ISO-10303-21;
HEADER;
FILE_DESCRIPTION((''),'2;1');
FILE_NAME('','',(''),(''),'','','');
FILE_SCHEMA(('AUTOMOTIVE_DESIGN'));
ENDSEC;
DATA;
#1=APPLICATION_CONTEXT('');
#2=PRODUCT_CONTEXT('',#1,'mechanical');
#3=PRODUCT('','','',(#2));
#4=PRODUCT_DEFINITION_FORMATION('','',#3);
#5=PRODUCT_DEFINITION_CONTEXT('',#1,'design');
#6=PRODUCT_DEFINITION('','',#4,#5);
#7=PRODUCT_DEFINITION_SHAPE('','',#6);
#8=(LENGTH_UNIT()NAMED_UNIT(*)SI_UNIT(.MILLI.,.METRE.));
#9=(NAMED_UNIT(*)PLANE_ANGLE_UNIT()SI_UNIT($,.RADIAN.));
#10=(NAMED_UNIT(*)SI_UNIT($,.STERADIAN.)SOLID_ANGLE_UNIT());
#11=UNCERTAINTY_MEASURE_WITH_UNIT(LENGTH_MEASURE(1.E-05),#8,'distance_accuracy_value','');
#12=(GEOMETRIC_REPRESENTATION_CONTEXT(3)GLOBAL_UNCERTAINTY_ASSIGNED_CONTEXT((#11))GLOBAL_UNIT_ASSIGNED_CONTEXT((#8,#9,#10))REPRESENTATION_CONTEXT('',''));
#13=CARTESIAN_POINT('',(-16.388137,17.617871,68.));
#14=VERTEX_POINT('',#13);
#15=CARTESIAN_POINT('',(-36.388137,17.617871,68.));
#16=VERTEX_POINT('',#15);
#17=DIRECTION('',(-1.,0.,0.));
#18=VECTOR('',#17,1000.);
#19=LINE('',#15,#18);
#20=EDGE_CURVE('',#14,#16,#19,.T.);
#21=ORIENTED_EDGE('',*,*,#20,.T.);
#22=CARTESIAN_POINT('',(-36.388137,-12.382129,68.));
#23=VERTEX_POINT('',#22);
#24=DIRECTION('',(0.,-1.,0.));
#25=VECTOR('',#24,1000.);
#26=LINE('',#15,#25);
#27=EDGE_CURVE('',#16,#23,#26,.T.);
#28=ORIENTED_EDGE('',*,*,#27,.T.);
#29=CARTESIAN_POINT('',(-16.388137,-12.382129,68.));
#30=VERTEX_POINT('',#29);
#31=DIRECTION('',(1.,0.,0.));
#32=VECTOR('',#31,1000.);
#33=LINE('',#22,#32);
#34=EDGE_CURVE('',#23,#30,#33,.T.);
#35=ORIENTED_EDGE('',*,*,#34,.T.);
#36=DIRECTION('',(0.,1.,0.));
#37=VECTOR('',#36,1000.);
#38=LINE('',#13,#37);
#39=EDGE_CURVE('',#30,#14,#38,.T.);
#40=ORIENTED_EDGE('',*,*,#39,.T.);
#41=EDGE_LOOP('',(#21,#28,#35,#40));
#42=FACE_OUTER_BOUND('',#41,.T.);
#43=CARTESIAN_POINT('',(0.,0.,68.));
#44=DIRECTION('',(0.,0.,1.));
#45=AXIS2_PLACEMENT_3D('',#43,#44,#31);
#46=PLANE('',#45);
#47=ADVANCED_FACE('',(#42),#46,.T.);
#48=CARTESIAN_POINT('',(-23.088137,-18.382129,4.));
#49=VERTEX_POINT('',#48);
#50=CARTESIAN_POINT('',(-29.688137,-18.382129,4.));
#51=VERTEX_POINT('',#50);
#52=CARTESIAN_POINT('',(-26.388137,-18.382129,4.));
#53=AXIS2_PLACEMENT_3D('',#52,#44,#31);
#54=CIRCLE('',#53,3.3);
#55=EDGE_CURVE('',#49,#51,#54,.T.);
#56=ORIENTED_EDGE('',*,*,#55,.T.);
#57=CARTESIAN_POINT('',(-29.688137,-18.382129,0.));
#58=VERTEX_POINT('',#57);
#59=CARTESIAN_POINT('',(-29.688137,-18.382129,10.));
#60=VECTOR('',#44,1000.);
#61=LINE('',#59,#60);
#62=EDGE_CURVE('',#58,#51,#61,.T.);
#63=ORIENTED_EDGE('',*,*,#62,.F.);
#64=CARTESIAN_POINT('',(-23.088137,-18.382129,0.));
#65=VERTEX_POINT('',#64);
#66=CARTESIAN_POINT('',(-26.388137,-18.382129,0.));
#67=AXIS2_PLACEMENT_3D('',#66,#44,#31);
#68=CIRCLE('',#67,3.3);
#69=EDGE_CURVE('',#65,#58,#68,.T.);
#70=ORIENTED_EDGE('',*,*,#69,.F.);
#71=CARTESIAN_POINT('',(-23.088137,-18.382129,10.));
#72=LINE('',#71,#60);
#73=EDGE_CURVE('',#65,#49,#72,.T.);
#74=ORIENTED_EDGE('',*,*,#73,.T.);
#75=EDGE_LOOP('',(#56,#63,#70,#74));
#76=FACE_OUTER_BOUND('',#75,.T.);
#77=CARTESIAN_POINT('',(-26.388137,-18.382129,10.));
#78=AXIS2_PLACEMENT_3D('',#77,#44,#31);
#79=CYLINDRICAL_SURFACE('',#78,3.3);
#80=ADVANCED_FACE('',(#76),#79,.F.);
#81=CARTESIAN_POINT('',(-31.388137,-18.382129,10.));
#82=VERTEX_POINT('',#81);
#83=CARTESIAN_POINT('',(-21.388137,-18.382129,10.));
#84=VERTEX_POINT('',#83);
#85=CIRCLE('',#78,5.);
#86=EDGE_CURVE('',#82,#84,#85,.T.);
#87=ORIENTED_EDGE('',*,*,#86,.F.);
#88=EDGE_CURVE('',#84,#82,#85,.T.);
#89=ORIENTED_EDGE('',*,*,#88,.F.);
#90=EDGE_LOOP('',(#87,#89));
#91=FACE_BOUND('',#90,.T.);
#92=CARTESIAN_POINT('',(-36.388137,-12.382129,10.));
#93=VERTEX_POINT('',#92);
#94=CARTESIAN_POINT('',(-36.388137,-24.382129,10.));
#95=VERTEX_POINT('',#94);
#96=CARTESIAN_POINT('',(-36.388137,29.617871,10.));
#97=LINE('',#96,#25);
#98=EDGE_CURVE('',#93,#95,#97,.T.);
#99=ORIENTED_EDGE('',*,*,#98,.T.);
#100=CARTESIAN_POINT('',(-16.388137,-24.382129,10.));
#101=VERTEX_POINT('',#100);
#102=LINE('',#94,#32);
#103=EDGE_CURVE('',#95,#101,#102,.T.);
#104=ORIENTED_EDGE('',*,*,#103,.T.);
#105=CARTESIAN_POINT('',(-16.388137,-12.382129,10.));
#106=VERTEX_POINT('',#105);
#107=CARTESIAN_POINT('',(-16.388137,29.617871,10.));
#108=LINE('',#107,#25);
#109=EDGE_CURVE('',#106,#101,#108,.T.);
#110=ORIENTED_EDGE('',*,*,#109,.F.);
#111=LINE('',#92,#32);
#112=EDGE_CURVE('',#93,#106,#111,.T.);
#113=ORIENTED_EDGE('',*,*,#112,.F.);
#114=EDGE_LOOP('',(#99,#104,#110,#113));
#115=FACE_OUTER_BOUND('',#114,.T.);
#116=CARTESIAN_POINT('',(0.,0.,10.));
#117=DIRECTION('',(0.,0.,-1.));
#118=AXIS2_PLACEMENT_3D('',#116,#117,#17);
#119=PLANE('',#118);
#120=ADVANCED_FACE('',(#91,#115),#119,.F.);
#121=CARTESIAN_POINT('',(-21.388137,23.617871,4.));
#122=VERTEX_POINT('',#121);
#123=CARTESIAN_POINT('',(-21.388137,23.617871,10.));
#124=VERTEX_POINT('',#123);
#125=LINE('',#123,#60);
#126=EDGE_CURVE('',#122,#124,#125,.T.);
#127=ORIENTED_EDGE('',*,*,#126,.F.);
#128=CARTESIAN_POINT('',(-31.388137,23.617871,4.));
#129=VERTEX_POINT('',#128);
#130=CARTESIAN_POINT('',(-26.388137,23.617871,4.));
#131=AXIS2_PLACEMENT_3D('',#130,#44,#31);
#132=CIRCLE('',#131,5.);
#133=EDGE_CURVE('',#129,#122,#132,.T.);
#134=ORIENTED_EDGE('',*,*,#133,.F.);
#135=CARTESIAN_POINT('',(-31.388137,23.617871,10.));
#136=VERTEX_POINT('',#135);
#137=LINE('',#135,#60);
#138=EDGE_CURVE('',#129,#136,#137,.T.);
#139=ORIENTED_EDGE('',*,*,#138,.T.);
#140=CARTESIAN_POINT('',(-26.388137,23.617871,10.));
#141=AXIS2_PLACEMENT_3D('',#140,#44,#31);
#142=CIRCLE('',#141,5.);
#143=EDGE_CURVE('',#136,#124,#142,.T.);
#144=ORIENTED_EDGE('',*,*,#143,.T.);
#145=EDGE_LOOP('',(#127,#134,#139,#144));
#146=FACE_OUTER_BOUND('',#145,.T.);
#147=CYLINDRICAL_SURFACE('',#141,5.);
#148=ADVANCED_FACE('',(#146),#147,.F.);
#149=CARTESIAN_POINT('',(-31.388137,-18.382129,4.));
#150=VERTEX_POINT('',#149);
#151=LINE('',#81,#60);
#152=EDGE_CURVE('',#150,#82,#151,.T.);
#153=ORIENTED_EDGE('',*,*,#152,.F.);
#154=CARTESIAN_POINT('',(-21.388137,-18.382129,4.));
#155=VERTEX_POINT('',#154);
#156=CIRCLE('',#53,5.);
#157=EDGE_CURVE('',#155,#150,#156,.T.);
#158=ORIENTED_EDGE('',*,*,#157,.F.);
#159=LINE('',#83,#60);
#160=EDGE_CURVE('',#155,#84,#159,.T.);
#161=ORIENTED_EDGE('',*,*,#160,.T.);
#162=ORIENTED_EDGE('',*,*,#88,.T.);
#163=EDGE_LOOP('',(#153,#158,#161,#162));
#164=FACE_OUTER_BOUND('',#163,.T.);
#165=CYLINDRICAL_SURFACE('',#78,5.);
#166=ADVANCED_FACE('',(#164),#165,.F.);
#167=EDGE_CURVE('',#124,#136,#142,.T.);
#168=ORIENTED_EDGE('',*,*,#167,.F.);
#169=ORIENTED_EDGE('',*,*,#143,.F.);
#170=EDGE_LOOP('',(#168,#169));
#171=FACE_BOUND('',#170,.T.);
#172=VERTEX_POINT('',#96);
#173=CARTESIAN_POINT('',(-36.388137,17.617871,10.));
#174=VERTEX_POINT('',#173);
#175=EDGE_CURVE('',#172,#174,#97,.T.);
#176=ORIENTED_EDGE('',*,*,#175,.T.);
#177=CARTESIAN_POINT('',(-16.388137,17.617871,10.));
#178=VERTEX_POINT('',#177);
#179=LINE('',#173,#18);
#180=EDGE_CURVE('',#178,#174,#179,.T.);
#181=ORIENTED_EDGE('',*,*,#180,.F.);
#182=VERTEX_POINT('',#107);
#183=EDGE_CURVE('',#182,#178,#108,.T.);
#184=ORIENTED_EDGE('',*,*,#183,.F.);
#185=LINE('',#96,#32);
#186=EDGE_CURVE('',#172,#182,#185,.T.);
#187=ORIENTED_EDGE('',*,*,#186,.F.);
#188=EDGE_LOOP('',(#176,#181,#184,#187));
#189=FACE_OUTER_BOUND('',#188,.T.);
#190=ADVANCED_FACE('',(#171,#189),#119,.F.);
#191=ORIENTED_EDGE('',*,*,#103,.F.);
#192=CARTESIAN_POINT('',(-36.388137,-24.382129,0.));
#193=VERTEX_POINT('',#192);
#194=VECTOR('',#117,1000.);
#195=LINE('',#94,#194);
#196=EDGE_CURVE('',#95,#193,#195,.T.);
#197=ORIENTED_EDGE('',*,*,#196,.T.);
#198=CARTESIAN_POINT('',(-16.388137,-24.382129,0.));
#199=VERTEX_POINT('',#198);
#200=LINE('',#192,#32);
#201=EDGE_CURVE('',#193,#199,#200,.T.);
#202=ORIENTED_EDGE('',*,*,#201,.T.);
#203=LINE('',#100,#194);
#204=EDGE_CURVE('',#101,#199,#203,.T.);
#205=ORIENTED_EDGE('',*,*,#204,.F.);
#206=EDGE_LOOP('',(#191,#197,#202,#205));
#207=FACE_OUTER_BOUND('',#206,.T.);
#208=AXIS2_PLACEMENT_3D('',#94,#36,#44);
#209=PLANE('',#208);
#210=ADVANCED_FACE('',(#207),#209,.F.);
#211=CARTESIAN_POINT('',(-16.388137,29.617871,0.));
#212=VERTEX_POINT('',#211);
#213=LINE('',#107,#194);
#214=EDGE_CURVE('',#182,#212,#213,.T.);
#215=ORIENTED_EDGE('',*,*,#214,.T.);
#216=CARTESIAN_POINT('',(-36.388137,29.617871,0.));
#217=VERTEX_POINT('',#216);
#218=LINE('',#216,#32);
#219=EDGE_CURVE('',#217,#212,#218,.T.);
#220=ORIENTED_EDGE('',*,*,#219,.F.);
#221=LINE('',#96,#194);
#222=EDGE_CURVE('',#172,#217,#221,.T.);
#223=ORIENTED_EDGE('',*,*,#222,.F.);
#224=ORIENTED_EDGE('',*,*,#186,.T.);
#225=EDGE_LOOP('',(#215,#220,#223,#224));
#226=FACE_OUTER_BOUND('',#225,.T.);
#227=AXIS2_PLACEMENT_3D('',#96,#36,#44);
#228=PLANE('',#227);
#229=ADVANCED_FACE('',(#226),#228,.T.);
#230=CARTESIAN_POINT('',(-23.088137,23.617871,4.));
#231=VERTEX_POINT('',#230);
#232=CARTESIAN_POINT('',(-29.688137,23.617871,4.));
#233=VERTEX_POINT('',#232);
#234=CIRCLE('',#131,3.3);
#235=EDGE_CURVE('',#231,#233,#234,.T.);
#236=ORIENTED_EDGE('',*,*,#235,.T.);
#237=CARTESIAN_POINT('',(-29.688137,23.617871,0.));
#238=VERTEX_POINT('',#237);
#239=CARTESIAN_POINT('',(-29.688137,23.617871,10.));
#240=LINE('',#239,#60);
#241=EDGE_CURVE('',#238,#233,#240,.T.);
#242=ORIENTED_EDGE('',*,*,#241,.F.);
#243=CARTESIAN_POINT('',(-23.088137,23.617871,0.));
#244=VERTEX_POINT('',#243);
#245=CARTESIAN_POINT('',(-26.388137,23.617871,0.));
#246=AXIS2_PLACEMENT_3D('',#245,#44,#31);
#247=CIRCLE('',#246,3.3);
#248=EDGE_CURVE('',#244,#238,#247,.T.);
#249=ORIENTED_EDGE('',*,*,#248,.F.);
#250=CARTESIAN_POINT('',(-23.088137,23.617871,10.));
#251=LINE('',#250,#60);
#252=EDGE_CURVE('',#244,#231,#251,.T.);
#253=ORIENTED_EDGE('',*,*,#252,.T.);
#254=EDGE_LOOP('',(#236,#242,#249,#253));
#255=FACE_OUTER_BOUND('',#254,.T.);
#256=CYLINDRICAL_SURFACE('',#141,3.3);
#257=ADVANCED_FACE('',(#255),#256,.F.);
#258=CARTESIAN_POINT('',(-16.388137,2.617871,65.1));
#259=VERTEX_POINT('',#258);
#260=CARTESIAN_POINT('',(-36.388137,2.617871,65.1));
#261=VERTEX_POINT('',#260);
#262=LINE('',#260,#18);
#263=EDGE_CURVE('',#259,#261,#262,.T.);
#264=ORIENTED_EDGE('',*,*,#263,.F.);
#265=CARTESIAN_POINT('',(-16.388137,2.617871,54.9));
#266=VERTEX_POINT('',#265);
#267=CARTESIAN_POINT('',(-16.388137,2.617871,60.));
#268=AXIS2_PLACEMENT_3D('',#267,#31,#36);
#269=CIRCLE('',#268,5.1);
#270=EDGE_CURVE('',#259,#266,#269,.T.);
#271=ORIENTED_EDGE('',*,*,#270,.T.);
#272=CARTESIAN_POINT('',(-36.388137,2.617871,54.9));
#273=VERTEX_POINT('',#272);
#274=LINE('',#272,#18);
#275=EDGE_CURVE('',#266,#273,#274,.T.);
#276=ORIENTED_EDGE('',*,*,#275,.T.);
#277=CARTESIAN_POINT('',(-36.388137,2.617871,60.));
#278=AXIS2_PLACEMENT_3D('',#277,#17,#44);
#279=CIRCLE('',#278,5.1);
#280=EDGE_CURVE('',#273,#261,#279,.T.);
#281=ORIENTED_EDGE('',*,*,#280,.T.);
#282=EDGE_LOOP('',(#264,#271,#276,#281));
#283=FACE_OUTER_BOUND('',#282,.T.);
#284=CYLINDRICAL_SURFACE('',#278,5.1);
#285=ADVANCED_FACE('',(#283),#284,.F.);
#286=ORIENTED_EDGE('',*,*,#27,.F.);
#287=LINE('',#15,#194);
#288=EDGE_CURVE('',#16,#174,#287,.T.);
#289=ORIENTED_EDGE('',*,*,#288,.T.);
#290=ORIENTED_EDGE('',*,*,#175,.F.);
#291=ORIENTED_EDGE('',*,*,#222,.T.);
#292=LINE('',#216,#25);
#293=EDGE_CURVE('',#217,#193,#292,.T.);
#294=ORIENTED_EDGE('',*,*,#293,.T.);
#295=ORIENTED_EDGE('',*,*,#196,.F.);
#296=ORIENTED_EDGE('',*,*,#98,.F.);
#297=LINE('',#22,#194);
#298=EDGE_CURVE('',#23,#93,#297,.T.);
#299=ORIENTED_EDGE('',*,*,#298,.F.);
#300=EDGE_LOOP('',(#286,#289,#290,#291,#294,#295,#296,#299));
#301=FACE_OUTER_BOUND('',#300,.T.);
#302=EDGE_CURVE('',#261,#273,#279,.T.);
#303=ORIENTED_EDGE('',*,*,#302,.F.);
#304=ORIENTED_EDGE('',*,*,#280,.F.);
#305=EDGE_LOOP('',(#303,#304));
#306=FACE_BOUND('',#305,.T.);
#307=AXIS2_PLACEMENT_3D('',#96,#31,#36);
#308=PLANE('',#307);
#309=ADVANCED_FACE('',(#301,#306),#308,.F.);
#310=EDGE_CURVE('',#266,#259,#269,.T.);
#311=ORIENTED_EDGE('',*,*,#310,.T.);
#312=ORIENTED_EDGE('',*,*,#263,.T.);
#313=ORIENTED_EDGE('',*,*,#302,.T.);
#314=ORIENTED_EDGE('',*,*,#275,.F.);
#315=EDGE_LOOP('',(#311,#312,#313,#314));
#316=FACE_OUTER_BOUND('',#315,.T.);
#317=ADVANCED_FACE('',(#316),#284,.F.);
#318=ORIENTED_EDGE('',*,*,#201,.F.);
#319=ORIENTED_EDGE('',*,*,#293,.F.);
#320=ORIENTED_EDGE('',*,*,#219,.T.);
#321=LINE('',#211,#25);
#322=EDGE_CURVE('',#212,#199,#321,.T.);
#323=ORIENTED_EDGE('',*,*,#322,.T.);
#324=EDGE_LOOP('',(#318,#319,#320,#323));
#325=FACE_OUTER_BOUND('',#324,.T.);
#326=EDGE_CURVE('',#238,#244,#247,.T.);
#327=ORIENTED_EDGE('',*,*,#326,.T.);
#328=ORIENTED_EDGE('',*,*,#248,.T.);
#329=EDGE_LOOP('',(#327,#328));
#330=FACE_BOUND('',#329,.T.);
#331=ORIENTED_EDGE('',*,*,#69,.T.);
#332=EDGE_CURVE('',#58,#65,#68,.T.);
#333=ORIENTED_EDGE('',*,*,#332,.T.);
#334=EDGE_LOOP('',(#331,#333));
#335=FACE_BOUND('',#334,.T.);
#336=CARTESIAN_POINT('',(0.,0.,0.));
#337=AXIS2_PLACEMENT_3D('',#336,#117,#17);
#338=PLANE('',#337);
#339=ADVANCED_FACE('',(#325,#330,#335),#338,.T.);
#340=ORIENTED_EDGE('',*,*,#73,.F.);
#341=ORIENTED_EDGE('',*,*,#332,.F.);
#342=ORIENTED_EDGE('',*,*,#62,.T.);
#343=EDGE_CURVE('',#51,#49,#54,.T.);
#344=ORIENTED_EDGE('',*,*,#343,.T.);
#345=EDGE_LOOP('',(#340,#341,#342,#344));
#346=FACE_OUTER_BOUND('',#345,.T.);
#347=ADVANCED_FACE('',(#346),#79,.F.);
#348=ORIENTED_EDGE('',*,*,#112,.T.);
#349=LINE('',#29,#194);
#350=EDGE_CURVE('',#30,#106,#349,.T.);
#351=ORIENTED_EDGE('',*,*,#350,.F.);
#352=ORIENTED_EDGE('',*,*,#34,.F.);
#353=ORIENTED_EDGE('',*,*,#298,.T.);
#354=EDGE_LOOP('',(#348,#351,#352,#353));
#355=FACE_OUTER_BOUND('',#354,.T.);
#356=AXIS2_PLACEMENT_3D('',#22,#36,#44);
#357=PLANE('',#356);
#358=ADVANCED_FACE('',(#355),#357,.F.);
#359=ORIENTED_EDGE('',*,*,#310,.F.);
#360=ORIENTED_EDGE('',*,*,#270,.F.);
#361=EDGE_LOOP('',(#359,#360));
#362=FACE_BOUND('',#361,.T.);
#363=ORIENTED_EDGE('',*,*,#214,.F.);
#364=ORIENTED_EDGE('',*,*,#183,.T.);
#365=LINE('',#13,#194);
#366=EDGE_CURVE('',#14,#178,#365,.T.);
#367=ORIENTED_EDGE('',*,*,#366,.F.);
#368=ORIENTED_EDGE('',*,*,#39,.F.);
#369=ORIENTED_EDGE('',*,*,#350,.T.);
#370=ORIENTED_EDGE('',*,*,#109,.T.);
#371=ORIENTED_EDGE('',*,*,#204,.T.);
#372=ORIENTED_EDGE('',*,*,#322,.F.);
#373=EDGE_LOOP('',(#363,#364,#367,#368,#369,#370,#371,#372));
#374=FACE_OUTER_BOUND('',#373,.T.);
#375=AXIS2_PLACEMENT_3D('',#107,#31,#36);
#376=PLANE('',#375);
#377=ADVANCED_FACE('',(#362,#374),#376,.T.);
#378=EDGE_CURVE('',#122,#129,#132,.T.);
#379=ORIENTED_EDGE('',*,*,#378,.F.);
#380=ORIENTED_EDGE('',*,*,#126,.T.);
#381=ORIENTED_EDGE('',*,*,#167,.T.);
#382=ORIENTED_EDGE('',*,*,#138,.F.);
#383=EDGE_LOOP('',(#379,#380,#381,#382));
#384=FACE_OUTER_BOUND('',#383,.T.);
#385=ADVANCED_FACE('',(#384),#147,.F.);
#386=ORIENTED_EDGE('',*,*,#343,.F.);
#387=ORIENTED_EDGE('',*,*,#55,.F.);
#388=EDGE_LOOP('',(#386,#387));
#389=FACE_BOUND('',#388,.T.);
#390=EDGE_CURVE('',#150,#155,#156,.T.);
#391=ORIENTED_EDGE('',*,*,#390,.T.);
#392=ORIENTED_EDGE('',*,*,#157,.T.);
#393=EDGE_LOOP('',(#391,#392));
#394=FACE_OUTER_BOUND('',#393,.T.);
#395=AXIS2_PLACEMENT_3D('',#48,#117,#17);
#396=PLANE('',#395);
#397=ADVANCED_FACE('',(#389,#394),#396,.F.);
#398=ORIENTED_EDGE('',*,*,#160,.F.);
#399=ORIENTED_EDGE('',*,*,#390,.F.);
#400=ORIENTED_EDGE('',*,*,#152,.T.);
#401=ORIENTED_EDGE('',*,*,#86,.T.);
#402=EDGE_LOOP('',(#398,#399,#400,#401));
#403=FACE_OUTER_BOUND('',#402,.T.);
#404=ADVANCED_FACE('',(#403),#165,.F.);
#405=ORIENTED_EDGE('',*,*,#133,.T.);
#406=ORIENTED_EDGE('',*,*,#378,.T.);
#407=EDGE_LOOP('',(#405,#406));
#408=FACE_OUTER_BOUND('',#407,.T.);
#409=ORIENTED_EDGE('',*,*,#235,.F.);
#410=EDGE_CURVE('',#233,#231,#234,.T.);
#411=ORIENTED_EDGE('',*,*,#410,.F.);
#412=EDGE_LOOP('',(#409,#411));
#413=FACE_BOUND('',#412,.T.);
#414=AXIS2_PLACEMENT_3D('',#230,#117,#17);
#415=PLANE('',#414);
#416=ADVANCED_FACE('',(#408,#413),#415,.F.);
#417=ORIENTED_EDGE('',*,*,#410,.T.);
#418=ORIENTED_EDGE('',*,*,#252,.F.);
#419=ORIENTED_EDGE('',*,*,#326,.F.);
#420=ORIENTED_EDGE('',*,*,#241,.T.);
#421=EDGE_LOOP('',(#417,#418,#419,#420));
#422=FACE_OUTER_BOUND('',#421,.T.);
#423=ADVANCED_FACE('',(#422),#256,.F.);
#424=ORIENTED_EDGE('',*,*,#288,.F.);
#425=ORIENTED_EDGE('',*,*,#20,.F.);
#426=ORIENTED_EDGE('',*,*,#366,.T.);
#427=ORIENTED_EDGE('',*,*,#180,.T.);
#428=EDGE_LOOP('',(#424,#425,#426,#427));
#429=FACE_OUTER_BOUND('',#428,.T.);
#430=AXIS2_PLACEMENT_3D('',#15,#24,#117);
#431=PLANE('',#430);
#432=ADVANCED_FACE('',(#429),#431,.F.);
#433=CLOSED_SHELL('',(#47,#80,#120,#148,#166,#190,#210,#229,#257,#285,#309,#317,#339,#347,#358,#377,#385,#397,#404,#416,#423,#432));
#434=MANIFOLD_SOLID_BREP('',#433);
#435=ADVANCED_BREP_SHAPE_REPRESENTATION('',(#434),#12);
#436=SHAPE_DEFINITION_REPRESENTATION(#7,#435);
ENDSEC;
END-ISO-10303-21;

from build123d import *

# Parameters (mm, degrees)
SKETCH1_W                               = 20
SKETCH1_H                               = 54
BOSS_EXTRUDE1_DEPTH                     = 10
SKETCH2_W                               = 20
SKETCH2_H                               = 30
BOSS_EXTRUDE2_DEPTH                     = 58
CBORE_FOR_M6_HEX_HEAD_BOLT1_D           = 6.6
CBORE_FOR_M6_HEX_HEAD_BOLT1_CBORE_D     = 10
CBORE_FOR_M6_HEX_HEAD_BOLT1_CBORE_DEPTH = 6
M12_TAPPED_HOLE1_D                      = 10.2


with BuildPart() as part:
    # Sketch1 → Boss-Extrude1 (new body)
    with BuildSketch(Plane.XY):
        with Locations((-26.388136882, 2.617870722)):
            Rectangle(SKETCH1_W, SKETCH1_H)
    extrude(amount=BOSS_EXTRUDE1_DEPTH)

    # Sketch2 → Boss-Extrude2 (add)
    with BuildSketch(Plane.XY.offset(10)):
        with Locations((-26.388136882, 2.617870722)):
            Rectangle(SKETCH2_W, SKETCH2_H)
    extrude(amount=BOSS_EXTRUDE2_DEPTH)

    # CBORE for M6 Hex Head Bolt1 (through all)
    with Locations(Plane.XY.offset(10)):
        with Locations((-26.388136882, 23.617870722), (-26.388136882, -18.382129278)):
            CounterBoreHole(CBORE_FOR_M6_HEX_HEAD_BOLT1_D / 2, CBORE_FOR_M6_HEX_HEAD_BOLT1_CBORE_D / 2, CBORE_FOR_M6_HEX_HEAD_BOLT1_CBORE_DEPTH)

    # M12 Tapped Hole1 (through all)
    with Locations(Plane.ZY.offset(36.388136882)):
        with Locations((60, 2.617870722)):
            Hole(M12_TAPPED_HOLE1_D / 2)


solid = part.part
